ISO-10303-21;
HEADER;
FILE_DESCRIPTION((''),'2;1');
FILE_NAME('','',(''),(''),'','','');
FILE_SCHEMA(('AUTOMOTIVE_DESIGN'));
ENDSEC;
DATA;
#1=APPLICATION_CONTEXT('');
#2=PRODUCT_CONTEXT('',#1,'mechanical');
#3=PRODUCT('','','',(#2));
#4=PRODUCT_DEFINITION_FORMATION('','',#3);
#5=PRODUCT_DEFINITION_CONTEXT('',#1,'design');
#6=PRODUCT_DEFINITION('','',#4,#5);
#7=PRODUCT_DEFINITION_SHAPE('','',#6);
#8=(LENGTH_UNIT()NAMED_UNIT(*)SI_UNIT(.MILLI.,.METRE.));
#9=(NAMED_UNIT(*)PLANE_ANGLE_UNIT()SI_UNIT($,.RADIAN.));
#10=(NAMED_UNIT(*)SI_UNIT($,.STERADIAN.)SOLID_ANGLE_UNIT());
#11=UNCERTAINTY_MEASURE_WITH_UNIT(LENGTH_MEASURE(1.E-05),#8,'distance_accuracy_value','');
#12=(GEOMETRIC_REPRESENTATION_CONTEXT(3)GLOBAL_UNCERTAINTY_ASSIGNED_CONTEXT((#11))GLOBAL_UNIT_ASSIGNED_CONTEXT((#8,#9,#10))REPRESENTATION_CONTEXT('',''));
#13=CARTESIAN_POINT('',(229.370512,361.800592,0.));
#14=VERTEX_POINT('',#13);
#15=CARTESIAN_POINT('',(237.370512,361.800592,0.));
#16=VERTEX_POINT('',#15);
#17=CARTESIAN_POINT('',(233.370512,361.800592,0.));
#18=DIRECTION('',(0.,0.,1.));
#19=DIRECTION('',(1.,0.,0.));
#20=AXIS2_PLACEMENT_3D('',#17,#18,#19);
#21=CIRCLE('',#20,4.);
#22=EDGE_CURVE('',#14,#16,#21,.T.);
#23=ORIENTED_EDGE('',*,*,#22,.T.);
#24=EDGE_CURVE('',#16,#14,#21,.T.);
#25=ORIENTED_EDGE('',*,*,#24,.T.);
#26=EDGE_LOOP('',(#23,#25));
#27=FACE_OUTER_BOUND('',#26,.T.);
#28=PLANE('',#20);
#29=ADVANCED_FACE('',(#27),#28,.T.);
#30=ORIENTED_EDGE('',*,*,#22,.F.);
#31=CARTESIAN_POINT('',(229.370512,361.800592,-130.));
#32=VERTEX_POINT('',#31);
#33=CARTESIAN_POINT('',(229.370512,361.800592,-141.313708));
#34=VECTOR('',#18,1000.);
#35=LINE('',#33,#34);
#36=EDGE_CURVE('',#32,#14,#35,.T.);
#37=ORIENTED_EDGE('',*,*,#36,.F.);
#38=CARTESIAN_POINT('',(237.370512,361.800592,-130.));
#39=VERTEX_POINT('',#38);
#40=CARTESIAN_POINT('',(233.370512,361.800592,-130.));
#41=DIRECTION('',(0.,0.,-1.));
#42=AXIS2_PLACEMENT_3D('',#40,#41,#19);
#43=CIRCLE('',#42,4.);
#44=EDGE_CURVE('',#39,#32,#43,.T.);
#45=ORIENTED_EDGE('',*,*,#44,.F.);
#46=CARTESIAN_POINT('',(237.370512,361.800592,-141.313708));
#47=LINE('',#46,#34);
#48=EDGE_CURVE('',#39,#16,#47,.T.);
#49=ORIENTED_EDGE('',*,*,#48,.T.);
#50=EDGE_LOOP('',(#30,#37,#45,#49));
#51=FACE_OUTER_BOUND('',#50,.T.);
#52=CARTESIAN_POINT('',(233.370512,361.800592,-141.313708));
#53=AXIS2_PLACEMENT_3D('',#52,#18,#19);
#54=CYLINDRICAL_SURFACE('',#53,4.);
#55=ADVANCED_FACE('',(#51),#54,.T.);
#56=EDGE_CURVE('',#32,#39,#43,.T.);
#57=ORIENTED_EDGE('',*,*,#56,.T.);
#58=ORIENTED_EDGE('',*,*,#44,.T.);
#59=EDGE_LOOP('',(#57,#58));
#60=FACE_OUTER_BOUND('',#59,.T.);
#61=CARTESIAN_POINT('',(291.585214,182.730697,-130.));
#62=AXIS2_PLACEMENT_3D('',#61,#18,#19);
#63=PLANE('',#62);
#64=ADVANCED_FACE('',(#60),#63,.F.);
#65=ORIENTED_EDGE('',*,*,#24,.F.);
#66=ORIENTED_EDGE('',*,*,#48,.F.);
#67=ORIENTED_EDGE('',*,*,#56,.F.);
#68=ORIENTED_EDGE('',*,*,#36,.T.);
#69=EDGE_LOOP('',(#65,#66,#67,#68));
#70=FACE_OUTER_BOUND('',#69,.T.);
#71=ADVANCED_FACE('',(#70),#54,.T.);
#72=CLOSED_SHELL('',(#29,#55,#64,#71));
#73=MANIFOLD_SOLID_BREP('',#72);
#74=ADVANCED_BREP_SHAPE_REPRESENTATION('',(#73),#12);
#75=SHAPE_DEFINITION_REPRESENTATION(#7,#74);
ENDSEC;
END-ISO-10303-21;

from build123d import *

# Parameters (mm, degrees)
SKETCH1_R           = 4
BOSS_EXTRUDE1_DEPTH = 130


with BuildPart() as part:
    # Sketch1 → Boss-Extrude1 (new body)
    with BuildSketch(Plane.XY):
        with Locations((233.370511684, 361.800592491)):
            Circle(SKETCH1_R)
    extrude(amount=-BOSS_EXTRUDE1_DEPTH)


solid = part.part
